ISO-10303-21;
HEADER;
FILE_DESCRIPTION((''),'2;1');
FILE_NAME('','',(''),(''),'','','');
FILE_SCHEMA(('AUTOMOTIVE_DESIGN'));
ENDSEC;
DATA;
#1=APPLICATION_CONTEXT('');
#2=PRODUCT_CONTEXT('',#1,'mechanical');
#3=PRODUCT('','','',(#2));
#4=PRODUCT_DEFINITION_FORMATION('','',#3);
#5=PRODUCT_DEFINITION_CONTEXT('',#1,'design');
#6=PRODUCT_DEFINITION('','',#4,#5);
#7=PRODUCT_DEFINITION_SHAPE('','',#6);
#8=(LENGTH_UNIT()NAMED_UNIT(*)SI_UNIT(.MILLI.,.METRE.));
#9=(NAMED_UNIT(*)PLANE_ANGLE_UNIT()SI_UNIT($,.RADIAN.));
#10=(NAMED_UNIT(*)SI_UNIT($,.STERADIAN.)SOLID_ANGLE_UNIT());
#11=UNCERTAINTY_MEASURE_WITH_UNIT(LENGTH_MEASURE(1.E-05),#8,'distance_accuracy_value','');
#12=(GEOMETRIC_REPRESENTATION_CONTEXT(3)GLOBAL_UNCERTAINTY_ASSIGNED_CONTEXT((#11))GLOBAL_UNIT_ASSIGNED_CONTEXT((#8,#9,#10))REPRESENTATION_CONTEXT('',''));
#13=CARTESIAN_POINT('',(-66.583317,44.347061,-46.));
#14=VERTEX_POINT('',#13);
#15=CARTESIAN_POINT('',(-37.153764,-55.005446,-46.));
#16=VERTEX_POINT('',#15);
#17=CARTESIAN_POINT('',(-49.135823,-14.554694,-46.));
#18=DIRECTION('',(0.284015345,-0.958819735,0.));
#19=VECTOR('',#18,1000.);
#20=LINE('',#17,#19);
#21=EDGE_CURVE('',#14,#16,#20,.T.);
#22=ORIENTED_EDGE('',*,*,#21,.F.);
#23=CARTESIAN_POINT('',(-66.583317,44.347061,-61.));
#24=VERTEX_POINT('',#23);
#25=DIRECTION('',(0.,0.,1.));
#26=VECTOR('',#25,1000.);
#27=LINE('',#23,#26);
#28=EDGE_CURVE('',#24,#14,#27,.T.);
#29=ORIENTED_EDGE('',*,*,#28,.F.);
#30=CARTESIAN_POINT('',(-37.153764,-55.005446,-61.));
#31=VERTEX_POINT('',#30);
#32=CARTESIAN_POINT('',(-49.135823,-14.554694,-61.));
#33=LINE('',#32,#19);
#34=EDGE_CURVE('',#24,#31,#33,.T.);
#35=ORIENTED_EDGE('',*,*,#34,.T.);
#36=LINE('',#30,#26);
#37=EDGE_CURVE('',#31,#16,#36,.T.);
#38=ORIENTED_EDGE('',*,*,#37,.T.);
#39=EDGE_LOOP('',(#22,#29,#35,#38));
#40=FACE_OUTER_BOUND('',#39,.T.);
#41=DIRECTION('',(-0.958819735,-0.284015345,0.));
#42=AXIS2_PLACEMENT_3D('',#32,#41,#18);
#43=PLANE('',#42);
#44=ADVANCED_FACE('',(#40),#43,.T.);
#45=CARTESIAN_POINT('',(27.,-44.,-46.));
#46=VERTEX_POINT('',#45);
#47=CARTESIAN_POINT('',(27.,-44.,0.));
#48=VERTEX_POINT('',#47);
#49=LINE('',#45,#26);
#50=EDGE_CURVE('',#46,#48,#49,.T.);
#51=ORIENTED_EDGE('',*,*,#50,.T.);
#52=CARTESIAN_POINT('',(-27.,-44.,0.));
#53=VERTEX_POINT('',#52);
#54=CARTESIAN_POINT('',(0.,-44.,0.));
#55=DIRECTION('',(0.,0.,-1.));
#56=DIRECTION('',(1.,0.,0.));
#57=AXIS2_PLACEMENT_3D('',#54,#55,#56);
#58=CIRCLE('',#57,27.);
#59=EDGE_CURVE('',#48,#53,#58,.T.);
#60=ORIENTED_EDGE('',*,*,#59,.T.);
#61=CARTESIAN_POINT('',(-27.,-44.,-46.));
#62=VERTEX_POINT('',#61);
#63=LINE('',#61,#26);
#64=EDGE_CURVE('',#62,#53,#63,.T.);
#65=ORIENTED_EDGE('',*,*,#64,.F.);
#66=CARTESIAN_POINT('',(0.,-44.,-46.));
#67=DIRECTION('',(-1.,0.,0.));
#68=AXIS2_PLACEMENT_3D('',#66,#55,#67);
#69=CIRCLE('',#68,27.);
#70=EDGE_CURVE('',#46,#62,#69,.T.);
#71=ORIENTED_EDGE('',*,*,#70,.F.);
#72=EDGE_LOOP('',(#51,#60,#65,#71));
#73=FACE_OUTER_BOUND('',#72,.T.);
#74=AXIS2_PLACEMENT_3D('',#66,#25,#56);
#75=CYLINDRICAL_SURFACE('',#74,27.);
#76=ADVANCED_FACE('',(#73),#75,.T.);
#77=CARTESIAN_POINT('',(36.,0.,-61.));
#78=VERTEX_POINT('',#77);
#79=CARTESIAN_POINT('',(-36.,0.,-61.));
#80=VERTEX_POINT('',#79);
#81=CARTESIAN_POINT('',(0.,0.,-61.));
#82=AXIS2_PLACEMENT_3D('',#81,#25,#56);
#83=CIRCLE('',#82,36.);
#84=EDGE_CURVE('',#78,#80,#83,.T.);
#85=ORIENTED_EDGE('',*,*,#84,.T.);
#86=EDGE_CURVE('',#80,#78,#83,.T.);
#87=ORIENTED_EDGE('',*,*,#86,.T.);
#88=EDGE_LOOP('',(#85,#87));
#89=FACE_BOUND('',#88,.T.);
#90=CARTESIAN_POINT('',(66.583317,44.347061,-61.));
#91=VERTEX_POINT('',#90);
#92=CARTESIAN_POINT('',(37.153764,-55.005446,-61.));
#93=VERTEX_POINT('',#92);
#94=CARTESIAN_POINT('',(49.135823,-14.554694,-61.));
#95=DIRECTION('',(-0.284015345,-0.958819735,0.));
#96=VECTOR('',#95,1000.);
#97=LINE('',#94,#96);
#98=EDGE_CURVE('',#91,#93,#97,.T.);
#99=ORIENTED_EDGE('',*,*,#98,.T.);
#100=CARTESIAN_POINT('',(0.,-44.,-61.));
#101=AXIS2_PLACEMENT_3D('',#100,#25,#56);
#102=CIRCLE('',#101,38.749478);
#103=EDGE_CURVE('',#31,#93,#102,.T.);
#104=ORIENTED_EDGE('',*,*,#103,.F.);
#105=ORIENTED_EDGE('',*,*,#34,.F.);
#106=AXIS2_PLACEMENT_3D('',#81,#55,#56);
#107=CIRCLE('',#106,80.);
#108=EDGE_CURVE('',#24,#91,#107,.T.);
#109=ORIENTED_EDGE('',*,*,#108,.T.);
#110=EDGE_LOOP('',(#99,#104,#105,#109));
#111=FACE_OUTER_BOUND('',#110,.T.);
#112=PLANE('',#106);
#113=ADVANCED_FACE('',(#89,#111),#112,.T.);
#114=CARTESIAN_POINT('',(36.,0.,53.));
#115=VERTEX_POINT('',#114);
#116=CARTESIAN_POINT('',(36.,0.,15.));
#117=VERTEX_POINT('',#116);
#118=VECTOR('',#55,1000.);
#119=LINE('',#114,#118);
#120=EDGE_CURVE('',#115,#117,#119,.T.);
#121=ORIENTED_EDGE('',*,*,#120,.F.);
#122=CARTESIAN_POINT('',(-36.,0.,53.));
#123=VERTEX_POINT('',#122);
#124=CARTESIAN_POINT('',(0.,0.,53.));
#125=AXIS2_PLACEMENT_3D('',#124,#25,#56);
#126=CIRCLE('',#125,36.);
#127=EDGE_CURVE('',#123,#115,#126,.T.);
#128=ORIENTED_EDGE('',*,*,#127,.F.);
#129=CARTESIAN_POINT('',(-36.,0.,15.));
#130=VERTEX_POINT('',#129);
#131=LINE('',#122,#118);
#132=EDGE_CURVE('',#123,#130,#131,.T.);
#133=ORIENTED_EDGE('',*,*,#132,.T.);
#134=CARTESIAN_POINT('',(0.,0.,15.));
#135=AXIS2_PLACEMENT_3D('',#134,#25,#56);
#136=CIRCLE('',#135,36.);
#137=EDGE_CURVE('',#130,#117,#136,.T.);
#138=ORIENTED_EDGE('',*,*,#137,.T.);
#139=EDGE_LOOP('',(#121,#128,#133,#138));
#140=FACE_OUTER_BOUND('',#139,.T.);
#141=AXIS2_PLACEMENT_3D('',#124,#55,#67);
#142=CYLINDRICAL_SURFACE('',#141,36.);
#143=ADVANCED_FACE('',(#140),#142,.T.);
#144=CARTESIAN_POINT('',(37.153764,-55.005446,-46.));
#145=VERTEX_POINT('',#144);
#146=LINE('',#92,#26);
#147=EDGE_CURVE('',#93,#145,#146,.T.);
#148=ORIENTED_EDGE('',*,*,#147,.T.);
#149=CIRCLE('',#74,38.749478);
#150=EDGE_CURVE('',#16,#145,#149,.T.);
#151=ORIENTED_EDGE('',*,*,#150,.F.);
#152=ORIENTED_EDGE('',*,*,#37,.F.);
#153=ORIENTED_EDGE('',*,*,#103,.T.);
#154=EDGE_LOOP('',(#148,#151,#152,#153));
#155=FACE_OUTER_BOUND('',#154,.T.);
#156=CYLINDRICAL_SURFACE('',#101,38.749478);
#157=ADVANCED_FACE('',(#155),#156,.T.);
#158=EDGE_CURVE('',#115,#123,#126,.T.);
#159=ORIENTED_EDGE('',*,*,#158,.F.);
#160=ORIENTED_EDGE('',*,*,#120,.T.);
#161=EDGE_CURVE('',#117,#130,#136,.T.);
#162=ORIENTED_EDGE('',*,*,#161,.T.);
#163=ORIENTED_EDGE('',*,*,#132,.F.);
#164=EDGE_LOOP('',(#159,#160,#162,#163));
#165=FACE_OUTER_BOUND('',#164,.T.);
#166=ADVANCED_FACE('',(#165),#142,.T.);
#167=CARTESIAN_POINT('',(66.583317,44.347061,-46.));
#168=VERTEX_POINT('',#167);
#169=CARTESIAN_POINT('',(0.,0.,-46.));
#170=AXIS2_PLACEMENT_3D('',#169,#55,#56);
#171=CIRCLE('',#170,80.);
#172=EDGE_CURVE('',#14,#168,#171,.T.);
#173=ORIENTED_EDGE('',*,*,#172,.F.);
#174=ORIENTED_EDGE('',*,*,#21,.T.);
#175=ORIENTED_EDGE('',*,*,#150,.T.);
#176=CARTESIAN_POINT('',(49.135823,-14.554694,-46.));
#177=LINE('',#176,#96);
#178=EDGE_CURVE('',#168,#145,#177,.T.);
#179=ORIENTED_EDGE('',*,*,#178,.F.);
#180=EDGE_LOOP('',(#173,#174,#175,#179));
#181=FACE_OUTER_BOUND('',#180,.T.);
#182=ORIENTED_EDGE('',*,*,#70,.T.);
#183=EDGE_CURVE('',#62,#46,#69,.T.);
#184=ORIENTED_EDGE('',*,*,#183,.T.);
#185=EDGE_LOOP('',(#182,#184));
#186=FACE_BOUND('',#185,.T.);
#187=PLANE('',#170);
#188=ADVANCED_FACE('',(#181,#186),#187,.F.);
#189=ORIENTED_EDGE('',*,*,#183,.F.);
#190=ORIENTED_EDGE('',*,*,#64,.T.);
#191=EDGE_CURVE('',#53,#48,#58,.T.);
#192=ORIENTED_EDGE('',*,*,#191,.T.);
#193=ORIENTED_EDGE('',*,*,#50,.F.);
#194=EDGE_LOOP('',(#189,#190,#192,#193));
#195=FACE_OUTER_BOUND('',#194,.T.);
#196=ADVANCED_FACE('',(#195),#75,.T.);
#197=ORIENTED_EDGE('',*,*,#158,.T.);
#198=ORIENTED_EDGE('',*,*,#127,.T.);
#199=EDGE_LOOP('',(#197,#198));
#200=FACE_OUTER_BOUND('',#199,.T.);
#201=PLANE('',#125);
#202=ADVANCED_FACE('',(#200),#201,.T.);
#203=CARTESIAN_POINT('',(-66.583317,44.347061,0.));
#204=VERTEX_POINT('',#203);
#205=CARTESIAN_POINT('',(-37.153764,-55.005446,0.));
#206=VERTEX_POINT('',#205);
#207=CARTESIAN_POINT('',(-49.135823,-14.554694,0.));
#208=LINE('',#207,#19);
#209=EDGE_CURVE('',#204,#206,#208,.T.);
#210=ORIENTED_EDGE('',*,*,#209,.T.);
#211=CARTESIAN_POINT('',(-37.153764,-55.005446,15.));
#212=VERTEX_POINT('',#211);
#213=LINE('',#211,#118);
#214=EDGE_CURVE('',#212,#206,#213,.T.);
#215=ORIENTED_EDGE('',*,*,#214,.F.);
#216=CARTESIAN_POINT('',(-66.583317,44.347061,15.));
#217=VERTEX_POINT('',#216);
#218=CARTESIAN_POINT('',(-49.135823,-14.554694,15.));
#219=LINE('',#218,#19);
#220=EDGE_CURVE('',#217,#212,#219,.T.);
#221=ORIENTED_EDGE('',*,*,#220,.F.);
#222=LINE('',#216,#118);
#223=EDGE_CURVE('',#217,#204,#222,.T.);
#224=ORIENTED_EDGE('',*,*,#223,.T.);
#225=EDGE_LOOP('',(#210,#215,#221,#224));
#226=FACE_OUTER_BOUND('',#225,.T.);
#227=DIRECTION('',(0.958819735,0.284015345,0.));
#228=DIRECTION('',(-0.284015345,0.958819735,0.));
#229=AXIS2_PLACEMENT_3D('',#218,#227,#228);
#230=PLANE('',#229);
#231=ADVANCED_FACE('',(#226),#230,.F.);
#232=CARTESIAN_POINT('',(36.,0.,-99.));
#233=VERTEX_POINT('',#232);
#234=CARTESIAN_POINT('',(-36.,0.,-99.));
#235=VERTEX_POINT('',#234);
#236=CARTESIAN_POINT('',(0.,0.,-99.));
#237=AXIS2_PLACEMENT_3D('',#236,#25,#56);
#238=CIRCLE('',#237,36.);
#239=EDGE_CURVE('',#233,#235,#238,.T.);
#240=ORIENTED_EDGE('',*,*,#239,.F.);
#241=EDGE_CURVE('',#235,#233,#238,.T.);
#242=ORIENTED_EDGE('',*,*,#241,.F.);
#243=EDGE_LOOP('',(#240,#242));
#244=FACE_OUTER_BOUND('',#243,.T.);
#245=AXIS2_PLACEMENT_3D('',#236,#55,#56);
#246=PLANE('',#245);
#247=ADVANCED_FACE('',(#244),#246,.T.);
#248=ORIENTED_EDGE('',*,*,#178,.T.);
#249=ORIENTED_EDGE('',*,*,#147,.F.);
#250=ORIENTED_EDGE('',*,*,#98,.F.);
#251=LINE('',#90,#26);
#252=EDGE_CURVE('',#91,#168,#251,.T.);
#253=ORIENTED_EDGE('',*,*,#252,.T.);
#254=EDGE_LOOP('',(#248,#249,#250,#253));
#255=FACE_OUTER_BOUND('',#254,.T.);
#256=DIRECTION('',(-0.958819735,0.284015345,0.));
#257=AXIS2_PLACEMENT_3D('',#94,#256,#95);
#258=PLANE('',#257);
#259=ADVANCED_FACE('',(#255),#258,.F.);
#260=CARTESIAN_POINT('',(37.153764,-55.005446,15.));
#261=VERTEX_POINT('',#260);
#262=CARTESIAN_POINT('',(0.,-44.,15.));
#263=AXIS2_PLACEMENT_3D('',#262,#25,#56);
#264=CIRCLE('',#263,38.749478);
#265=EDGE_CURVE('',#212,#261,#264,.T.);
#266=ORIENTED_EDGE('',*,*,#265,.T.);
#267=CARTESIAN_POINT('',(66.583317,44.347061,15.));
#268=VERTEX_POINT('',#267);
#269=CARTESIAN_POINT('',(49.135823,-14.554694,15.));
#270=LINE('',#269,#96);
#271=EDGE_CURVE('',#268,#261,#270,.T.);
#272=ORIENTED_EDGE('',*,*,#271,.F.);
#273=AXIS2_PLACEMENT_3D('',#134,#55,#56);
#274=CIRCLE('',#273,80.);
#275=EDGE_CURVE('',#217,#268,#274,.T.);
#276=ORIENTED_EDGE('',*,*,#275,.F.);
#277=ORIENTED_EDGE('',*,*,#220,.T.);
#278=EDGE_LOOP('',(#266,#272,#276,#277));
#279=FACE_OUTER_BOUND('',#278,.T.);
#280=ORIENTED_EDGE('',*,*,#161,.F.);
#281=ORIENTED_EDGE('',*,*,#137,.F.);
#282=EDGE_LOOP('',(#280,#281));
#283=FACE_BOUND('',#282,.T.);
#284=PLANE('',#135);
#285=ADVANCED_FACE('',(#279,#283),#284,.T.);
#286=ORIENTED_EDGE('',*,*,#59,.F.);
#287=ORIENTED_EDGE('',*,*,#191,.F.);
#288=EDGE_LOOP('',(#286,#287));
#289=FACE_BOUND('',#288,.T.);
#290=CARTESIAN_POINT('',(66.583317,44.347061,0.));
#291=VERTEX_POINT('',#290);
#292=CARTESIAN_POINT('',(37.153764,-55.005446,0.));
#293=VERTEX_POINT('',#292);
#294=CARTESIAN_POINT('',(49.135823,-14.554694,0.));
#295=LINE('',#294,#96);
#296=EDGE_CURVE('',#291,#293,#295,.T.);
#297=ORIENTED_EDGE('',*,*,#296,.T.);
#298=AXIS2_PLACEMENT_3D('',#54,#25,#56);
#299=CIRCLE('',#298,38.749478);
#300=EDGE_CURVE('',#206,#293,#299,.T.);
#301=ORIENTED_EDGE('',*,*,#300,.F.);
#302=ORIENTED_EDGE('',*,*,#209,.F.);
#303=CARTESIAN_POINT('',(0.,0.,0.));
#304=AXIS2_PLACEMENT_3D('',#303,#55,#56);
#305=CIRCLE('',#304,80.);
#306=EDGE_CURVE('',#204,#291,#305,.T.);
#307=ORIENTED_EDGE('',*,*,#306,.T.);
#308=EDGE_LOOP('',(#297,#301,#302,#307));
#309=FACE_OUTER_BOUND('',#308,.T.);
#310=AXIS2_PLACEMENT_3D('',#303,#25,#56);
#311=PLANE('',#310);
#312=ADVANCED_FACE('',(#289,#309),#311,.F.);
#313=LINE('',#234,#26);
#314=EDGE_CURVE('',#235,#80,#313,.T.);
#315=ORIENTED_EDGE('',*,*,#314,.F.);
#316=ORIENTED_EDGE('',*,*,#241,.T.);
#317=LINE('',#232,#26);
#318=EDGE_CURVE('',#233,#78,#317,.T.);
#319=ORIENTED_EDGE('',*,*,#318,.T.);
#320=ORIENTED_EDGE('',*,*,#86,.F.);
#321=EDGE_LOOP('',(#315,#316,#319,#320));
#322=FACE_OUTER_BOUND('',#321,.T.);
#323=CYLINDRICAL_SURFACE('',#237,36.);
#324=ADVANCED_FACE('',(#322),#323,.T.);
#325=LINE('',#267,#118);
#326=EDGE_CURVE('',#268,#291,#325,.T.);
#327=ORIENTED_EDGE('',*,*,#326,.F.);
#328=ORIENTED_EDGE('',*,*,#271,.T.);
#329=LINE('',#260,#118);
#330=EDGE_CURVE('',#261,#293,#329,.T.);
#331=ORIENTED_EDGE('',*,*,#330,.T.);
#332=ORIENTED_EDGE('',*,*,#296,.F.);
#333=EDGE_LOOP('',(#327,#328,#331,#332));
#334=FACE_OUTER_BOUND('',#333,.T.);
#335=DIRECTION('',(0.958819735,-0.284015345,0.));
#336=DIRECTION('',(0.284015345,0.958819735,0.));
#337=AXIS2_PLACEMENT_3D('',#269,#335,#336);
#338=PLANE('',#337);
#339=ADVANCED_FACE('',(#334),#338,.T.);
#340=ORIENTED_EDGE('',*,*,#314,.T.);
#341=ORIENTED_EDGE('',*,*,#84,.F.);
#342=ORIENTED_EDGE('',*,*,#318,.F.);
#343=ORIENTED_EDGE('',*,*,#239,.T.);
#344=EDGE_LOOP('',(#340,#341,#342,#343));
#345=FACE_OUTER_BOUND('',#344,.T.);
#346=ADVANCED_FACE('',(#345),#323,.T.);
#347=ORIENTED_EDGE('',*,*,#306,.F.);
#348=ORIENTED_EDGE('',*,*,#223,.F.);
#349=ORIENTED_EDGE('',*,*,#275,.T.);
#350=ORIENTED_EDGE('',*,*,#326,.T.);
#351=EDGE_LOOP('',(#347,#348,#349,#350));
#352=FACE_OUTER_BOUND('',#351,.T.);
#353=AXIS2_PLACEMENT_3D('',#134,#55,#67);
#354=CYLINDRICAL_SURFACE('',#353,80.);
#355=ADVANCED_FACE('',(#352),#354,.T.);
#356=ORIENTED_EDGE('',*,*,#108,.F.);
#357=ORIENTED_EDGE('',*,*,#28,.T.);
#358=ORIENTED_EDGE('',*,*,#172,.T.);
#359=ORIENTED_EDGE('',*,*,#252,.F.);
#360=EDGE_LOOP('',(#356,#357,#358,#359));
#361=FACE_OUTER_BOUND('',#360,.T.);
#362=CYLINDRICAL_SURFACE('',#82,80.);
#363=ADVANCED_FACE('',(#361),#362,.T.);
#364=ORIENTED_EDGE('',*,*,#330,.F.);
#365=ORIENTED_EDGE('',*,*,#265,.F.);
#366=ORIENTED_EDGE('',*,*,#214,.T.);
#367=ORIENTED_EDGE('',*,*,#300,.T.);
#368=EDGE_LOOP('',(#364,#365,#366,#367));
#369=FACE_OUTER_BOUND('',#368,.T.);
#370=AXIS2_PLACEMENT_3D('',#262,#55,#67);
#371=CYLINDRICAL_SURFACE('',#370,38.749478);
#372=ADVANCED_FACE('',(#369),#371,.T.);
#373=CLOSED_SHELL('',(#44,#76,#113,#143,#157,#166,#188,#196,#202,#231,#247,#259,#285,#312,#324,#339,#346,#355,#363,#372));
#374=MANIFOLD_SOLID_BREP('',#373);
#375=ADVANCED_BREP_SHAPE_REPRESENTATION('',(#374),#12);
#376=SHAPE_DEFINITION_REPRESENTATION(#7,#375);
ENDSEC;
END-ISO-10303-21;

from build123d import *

# Parameters (mm, degrees)
CRANK_WEB_DEPTH        = 15
CRANKPIN_PROFILE_R     = 27
CRANKPIN_DEPTH         = 46
MAIN_JOURNAL_PROFILE_R = 36
MAIN_JOURNAL_DEPTH     = 38


with BuildPart() as part:
    # Crank Web Profile → Crank Web (new body)
    with BuildSketch(Plane.XY):
        with BuildLine():
            ThreePointArc((66.583317356, 44.347061344), (0, 80), (-66.583317356, 44.347061344))
            Line((-66.583317356, 44.347061344), (-37.153763851, -55.005446241))
            ThreePointArc((-37.153763851, -55.005446241), (0, -82.749477613), (37.153763851, -55.005446241))
            Line((37.153763851, -55.005446241), (66.583317356, 44.347061344))
        make_face()
    crank_web = extrude(amount=CRANK_WEB_DEPTH)

    # Crankpin Profile → Crankpin (add)
    with BuildSketch(Plane(origin=(0, 0, 0), x_dir=(-1, 0, 0), z_dir=(0, 0, -1))):
        with Locations(Location((0, -44, 0), (0, 0, 180))):
            Circle(CRANKPIN_PROFILE_R)
    extrude(amount=CRANKPIN_DEPTH)

    # Main Journal Profile → Main Journal (add)
    with BuildSketch(Plane.XY.offset(15)):
        Circle(MAIN_JOURNAL_PROFILE_R)
    main_journal = extrude(amount=MAIN_JOURNAL_DEPTH)

    # Mirrored Web and Journal: Crank Web, Main Journal across plane
    add(crank_web.mirror(Plane(origin=(0, 0, -23), x_dir=(1, 0, 0), z_dir=(0, 0, -1))))
    add(main_journal.mirror(Plane(origin=(0, 0, -23), x_dir=(1, 0, 0), z_dir=(0, 0, -1))))


solid = part.part
